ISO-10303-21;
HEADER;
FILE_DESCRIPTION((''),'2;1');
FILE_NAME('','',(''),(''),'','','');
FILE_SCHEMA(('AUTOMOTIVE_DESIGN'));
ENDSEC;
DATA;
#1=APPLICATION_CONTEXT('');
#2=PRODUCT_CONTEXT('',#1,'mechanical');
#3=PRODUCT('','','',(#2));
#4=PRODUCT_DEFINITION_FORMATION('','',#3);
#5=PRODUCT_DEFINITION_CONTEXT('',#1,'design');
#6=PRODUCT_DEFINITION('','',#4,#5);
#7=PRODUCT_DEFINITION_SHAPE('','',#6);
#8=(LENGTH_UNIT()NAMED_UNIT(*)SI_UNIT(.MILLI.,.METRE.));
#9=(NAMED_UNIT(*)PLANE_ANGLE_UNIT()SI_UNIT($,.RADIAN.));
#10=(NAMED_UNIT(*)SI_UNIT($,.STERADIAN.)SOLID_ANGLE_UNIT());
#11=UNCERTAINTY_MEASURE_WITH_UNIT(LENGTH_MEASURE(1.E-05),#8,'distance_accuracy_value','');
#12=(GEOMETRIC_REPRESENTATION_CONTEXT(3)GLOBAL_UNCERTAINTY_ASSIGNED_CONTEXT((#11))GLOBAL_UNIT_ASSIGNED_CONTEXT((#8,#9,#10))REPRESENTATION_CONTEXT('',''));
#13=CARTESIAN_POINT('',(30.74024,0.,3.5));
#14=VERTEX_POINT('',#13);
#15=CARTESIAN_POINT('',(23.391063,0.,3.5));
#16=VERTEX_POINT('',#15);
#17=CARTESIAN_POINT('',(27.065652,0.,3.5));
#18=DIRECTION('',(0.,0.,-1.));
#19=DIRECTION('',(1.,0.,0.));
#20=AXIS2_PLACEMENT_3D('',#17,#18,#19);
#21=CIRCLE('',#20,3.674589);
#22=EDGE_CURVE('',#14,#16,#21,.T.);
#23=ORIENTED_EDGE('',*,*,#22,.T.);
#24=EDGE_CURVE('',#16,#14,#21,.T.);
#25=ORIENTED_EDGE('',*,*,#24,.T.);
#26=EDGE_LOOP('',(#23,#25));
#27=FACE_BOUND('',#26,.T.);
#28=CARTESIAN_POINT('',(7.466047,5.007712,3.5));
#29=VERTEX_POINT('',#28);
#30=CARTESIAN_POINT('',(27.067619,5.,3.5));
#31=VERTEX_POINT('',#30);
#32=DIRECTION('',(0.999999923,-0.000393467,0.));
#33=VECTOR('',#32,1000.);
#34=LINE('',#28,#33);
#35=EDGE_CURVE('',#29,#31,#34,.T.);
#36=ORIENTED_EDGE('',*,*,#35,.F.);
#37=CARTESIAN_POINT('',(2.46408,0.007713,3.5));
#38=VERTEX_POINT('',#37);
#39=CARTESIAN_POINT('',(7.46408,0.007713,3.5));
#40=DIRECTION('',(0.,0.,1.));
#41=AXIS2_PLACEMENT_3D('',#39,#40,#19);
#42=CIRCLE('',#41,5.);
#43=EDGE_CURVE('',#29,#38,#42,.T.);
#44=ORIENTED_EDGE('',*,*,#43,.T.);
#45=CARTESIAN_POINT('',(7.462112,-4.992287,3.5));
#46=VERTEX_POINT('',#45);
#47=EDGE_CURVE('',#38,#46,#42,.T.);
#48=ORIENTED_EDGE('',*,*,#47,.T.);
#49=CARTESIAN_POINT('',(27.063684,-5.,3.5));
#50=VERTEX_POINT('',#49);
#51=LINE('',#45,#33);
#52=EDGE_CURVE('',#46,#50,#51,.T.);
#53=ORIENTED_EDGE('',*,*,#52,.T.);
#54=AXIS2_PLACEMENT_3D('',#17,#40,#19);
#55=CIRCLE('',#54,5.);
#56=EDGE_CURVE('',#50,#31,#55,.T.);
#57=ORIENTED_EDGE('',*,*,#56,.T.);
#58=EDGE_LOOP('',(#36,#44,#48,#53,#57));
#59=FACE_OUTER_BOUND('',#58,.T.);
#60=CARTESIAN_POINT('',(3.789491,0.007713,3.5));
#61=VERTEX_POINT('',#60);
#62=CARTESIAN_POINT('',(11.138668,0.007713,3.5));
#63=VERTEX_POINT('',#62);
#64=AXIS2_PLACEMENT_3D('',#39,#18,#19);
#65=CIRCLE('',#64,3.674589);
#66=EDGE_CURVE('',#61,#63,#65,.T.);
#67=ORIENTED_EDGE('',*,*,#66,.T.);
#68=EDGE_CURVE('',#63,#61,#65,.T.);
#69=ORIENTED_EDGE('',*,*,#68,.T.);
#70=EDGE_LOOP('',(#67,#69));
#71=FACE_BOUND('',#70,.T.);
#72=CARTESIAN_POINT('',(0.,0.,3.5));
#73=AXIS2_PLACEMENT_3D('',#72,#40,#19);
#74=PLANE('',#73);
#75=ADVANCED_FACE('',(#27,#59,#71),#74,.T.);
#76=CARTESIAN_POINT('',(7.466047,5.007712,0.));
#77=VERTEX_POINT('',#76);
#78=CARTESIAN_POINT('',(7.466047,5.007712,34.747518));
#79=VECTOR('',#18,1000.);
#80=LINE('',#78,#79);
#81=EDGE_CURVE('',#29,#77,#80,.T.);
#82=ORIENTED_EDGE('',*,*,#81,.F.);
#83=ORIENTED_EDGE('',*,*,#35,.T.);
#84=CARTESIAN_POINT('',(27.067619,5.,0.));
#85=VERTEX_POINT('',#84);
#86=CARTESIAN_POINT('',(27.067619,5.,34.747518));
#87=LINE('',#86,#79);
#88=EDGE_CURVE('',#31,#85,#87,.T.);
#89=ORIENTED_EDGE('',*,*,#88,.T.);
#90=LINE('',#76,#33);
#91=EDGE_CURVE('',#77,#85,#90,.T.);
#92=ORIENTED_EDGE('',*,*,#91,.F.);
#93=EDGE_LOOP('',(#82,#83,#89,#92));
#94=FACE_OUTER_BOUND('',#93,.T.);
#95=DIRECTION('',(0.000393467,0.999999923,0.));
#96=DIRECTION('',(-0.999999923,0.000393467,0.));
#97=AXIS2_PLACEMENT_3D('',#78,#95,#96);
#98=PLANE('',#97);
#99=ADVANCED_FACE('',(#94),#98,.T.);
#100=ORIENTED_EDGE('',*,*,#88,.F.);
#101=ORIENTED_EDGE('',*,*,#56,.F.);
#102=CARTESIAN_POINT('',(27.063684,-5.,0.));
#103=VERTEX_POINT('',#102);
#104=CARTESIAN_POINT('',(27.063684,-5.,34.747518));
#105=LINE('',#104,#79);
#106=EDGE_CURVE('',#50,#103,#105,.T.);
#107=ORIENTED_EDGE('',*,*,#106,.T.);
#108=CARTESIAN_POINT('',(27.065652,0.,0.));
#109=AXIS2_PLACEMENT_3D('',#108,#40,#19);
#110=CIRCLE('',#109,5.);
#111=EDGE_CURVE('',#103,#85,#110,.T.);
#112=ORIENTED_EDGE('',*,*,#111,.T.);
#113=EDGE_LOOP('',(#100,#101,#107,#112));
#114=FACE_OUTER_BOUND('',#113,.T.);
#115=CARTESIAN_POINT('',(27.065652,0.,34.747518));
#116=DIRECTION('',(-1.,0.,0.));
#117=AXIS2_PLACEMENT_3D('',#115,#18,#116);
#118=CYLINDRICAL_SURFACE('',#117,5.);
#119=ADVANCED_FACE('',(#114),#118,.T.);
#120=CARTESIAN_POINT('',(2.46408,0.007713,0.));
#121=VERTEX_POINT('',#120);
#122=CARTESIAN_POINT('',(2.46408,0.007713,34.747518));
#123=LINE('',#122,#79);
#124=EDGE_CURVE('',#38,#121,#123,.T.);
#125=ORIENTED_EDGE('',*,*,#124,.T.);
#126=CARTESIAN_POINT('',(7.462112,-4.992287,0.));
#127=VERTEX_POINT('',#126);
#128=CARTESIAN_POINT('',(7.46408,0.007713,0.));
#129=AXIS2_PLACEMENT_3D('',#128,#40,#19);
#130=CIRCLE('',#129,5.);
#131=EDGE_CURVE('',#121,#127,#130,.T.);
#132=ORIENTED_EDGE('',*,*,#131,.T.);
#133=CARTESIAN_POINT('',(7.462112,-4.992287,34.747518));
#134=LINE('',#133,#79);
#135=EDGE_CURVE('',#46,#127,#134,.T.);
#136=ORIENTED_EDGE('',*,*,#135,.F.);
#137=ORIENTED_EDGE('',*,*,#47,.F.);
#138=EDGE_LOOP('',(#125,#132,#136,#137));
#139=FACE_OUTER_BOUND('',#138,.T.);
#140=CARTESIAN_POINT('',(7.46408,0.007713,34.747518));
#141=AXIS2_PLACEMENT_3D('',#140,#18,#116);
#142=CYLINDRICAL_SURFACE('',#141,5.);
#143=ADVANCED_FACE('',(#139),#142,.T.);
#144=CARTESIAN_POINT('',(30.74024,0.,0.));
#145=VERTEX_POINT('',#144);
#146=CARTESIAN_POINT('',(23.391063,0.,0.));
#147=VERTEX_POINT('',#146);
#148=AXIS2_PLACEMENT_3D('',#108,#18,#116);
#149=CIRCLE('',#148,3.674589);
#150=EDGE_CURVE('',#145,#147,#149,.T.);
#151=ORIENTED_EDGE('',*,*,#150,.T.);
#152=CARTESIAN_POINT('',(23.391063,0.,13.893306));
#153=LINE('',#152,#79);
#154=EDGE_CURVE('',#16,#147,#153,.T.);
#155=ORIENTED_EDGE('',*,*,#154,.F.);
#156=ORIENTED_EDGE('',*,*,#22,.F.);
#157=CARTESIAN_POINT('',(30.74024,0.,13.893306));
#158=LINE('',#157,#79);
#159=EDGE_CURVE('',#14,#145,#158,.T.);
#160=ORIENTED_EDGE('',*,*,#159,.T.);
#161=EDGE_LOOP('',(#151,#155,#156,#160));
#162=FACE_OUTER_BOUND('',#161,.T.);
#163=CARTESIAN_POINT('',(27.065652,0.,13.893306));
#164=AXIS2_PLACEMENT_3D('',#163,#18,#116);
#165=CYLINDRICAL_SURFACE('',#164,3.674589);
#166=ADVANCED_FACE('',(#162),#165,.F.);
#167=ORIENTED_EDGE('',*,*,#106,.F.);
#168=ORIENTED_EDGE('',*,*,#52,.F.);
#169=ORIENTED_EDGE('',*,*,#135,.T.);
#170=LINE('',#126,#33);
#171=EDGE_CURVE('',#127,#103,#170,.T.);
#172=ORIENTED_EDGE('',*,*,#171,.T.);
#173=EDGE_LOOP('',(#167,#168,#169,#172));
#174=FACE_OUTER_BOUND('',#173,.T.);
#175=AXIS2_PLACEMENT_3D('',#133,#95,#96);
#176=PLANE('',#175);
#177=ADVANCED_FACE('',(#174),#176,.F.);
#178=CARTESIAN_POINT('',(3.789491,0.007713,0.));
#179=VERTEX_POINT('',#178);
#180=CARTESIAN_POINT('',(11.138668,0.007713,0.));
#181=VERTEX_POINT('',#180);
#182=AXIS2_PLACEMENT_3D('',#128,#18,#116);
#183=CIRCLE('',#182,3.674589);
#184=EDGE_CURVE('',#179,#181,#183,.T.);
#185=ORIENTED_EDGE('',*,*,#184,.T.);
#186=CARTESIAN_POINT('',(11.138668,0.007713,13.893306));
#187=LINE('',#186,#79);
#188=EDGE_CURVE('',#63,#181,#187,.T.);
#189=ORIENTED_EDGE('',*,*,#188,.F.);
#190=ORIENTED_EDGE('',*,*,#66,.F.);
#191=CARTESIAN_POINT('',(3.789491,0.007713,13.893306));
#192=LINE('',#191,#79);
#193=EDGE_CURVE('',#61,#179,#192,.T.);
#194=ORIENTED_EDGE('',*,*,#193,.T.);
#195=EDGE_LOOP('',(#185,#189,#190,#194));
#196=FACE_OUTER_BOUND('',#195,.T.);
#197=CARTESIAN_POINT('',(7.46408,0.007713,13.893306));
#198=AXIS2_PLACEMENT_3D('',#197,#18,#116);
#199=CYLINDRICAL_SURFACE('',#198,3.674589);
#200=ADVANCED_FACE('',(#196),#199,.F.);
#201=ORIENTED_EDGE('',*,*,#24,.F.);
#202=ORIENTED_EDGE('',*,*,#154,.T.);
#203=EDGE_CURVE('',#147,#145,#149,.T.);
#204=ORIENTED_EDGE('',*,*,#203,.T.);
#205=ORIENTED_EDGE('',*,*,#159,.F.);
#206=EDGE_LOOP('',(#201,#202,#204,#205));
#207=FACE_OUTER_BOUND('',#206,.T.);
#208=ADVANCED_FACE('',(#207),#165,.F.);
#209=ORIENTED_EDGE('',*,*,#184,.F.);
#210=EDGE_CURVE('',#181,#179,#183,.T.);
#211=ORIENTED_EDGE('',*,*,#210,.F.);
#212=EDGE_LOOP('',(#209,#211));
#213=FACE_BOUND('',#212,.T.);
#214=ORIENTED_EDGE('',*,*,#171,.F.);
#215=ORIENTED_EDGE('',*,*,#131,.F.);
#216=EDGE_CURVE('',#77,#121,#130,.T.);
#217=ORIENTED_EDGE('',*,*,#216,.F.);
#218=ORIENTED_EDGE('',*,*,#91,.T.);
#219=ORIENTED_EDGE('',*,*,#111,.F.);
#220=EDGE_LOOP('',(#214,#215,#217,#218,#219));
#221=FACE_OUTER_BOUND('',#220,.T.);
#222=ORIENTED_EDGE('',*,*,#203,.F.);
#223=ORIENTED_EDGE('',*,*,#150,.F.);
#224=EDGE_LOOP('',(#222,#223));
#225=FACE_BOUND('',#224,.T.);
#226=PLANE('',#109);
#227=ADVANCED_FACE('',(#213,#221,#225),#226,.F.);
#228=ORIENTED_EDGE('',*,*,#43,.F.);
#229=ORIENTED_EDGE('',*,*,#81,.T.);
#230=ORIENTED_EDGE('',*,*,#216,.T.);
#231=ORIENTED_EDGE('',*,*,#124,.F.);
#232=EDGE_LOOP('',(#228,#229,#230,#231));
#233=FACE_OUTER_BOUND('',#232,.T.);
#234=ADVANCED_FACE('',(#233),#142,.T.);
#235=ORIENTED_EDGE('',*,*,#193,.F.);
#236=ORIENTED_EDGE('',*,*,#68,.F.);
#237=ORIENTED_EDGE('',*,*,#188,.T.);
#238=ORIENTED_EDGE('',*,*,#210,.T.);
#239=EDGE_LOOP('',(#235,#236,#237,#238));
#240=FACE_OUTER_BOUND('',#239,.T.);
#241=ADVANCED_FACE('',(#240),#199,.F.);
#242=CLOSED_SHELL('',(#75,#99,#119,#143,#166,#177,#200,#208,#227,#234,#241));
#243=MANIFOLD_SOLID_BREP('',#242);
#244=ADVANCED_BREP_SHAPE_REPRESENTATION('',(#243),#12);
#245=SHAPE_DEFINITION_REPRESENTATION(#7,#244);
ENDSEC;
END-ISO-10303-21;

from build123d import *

# Parameters (mm, degrees)
BOSS_EXTRUDE1_DEPTH = 3.5
CUT_EXTRUDE1_REACH  = 34.643
SKETCH2_R           = 3.674588618


with BuildPart() as part:
    # Sketch1 → Boss-Extrude1 (new body)
    with BuildSketch(Plane.XY):
        with BuildLine():
            Line((7.466046977, 5.007712178), (27.067619065, 4.999999613))
            ThreePointArc((27.067619065, 4.999999613), (32.065651345, -0.001967333), (27.063684399, -4.999999613))
            Line((27.063684399, -4.999999613), (7.462112311, -4.992287048))
            ThreePointArc((7.462112311, -4.992287048), (2.464080031, 0.009679898), (7.466046977, 5.007712178))
        make_face()
    extrude(amount=BOSS_EXTRUDE1_DEPTH)

    # Sketch2 → Cut-Extrude1 (cut, up to next)
    with BuildSketch(Plane(origin=(0, 0, 0), x_dir=(-1, 0, 0), z_dir=(0, 0, -1)), mode=Mode.PRIVATE) as cut_extrude1_sk1:
        with Locations((-27.065651732, 0)):
            Circle(SKETCH2_R)
    cut_extrude1_tool1 = extrude(cut_extrude1_sk1.sketch, amount=-CUT_EXTRUDE1_REACH, mode=Mode.PRIVATE) & part.part
    # Sketch2 → Cut-Extrude1 (cut, up to next)
    with BuildSketch(Plane(origin=(0, 0, 0), x_dir=(-1, 0, 0), z_dir=(0, 0, -1)), mode=Mode.PRIVATE) as cut_extrude1_sk2:
        with Locations((-7.464079644, 0.007712565)):
            Circle(SKETCH2_R)
    cut_extrude1_tool2 = extrude(cut_extrude1_sk2.sketch, amount=-CUT_EXTRUDE1_REACH, mode=Mode.PRIVATE) & part.part
    add(cut_extrude1_tool1.solids().sort_by_distance((27.065652, 0, 0))[0], mode=Mode.SUBTRACT)
    add(cut_extrude1_tool2.solids().sort_by_distance((7.46408, 0.007713, 0))[0], mode=Mode.SUBTRACT)


solid = part.part
